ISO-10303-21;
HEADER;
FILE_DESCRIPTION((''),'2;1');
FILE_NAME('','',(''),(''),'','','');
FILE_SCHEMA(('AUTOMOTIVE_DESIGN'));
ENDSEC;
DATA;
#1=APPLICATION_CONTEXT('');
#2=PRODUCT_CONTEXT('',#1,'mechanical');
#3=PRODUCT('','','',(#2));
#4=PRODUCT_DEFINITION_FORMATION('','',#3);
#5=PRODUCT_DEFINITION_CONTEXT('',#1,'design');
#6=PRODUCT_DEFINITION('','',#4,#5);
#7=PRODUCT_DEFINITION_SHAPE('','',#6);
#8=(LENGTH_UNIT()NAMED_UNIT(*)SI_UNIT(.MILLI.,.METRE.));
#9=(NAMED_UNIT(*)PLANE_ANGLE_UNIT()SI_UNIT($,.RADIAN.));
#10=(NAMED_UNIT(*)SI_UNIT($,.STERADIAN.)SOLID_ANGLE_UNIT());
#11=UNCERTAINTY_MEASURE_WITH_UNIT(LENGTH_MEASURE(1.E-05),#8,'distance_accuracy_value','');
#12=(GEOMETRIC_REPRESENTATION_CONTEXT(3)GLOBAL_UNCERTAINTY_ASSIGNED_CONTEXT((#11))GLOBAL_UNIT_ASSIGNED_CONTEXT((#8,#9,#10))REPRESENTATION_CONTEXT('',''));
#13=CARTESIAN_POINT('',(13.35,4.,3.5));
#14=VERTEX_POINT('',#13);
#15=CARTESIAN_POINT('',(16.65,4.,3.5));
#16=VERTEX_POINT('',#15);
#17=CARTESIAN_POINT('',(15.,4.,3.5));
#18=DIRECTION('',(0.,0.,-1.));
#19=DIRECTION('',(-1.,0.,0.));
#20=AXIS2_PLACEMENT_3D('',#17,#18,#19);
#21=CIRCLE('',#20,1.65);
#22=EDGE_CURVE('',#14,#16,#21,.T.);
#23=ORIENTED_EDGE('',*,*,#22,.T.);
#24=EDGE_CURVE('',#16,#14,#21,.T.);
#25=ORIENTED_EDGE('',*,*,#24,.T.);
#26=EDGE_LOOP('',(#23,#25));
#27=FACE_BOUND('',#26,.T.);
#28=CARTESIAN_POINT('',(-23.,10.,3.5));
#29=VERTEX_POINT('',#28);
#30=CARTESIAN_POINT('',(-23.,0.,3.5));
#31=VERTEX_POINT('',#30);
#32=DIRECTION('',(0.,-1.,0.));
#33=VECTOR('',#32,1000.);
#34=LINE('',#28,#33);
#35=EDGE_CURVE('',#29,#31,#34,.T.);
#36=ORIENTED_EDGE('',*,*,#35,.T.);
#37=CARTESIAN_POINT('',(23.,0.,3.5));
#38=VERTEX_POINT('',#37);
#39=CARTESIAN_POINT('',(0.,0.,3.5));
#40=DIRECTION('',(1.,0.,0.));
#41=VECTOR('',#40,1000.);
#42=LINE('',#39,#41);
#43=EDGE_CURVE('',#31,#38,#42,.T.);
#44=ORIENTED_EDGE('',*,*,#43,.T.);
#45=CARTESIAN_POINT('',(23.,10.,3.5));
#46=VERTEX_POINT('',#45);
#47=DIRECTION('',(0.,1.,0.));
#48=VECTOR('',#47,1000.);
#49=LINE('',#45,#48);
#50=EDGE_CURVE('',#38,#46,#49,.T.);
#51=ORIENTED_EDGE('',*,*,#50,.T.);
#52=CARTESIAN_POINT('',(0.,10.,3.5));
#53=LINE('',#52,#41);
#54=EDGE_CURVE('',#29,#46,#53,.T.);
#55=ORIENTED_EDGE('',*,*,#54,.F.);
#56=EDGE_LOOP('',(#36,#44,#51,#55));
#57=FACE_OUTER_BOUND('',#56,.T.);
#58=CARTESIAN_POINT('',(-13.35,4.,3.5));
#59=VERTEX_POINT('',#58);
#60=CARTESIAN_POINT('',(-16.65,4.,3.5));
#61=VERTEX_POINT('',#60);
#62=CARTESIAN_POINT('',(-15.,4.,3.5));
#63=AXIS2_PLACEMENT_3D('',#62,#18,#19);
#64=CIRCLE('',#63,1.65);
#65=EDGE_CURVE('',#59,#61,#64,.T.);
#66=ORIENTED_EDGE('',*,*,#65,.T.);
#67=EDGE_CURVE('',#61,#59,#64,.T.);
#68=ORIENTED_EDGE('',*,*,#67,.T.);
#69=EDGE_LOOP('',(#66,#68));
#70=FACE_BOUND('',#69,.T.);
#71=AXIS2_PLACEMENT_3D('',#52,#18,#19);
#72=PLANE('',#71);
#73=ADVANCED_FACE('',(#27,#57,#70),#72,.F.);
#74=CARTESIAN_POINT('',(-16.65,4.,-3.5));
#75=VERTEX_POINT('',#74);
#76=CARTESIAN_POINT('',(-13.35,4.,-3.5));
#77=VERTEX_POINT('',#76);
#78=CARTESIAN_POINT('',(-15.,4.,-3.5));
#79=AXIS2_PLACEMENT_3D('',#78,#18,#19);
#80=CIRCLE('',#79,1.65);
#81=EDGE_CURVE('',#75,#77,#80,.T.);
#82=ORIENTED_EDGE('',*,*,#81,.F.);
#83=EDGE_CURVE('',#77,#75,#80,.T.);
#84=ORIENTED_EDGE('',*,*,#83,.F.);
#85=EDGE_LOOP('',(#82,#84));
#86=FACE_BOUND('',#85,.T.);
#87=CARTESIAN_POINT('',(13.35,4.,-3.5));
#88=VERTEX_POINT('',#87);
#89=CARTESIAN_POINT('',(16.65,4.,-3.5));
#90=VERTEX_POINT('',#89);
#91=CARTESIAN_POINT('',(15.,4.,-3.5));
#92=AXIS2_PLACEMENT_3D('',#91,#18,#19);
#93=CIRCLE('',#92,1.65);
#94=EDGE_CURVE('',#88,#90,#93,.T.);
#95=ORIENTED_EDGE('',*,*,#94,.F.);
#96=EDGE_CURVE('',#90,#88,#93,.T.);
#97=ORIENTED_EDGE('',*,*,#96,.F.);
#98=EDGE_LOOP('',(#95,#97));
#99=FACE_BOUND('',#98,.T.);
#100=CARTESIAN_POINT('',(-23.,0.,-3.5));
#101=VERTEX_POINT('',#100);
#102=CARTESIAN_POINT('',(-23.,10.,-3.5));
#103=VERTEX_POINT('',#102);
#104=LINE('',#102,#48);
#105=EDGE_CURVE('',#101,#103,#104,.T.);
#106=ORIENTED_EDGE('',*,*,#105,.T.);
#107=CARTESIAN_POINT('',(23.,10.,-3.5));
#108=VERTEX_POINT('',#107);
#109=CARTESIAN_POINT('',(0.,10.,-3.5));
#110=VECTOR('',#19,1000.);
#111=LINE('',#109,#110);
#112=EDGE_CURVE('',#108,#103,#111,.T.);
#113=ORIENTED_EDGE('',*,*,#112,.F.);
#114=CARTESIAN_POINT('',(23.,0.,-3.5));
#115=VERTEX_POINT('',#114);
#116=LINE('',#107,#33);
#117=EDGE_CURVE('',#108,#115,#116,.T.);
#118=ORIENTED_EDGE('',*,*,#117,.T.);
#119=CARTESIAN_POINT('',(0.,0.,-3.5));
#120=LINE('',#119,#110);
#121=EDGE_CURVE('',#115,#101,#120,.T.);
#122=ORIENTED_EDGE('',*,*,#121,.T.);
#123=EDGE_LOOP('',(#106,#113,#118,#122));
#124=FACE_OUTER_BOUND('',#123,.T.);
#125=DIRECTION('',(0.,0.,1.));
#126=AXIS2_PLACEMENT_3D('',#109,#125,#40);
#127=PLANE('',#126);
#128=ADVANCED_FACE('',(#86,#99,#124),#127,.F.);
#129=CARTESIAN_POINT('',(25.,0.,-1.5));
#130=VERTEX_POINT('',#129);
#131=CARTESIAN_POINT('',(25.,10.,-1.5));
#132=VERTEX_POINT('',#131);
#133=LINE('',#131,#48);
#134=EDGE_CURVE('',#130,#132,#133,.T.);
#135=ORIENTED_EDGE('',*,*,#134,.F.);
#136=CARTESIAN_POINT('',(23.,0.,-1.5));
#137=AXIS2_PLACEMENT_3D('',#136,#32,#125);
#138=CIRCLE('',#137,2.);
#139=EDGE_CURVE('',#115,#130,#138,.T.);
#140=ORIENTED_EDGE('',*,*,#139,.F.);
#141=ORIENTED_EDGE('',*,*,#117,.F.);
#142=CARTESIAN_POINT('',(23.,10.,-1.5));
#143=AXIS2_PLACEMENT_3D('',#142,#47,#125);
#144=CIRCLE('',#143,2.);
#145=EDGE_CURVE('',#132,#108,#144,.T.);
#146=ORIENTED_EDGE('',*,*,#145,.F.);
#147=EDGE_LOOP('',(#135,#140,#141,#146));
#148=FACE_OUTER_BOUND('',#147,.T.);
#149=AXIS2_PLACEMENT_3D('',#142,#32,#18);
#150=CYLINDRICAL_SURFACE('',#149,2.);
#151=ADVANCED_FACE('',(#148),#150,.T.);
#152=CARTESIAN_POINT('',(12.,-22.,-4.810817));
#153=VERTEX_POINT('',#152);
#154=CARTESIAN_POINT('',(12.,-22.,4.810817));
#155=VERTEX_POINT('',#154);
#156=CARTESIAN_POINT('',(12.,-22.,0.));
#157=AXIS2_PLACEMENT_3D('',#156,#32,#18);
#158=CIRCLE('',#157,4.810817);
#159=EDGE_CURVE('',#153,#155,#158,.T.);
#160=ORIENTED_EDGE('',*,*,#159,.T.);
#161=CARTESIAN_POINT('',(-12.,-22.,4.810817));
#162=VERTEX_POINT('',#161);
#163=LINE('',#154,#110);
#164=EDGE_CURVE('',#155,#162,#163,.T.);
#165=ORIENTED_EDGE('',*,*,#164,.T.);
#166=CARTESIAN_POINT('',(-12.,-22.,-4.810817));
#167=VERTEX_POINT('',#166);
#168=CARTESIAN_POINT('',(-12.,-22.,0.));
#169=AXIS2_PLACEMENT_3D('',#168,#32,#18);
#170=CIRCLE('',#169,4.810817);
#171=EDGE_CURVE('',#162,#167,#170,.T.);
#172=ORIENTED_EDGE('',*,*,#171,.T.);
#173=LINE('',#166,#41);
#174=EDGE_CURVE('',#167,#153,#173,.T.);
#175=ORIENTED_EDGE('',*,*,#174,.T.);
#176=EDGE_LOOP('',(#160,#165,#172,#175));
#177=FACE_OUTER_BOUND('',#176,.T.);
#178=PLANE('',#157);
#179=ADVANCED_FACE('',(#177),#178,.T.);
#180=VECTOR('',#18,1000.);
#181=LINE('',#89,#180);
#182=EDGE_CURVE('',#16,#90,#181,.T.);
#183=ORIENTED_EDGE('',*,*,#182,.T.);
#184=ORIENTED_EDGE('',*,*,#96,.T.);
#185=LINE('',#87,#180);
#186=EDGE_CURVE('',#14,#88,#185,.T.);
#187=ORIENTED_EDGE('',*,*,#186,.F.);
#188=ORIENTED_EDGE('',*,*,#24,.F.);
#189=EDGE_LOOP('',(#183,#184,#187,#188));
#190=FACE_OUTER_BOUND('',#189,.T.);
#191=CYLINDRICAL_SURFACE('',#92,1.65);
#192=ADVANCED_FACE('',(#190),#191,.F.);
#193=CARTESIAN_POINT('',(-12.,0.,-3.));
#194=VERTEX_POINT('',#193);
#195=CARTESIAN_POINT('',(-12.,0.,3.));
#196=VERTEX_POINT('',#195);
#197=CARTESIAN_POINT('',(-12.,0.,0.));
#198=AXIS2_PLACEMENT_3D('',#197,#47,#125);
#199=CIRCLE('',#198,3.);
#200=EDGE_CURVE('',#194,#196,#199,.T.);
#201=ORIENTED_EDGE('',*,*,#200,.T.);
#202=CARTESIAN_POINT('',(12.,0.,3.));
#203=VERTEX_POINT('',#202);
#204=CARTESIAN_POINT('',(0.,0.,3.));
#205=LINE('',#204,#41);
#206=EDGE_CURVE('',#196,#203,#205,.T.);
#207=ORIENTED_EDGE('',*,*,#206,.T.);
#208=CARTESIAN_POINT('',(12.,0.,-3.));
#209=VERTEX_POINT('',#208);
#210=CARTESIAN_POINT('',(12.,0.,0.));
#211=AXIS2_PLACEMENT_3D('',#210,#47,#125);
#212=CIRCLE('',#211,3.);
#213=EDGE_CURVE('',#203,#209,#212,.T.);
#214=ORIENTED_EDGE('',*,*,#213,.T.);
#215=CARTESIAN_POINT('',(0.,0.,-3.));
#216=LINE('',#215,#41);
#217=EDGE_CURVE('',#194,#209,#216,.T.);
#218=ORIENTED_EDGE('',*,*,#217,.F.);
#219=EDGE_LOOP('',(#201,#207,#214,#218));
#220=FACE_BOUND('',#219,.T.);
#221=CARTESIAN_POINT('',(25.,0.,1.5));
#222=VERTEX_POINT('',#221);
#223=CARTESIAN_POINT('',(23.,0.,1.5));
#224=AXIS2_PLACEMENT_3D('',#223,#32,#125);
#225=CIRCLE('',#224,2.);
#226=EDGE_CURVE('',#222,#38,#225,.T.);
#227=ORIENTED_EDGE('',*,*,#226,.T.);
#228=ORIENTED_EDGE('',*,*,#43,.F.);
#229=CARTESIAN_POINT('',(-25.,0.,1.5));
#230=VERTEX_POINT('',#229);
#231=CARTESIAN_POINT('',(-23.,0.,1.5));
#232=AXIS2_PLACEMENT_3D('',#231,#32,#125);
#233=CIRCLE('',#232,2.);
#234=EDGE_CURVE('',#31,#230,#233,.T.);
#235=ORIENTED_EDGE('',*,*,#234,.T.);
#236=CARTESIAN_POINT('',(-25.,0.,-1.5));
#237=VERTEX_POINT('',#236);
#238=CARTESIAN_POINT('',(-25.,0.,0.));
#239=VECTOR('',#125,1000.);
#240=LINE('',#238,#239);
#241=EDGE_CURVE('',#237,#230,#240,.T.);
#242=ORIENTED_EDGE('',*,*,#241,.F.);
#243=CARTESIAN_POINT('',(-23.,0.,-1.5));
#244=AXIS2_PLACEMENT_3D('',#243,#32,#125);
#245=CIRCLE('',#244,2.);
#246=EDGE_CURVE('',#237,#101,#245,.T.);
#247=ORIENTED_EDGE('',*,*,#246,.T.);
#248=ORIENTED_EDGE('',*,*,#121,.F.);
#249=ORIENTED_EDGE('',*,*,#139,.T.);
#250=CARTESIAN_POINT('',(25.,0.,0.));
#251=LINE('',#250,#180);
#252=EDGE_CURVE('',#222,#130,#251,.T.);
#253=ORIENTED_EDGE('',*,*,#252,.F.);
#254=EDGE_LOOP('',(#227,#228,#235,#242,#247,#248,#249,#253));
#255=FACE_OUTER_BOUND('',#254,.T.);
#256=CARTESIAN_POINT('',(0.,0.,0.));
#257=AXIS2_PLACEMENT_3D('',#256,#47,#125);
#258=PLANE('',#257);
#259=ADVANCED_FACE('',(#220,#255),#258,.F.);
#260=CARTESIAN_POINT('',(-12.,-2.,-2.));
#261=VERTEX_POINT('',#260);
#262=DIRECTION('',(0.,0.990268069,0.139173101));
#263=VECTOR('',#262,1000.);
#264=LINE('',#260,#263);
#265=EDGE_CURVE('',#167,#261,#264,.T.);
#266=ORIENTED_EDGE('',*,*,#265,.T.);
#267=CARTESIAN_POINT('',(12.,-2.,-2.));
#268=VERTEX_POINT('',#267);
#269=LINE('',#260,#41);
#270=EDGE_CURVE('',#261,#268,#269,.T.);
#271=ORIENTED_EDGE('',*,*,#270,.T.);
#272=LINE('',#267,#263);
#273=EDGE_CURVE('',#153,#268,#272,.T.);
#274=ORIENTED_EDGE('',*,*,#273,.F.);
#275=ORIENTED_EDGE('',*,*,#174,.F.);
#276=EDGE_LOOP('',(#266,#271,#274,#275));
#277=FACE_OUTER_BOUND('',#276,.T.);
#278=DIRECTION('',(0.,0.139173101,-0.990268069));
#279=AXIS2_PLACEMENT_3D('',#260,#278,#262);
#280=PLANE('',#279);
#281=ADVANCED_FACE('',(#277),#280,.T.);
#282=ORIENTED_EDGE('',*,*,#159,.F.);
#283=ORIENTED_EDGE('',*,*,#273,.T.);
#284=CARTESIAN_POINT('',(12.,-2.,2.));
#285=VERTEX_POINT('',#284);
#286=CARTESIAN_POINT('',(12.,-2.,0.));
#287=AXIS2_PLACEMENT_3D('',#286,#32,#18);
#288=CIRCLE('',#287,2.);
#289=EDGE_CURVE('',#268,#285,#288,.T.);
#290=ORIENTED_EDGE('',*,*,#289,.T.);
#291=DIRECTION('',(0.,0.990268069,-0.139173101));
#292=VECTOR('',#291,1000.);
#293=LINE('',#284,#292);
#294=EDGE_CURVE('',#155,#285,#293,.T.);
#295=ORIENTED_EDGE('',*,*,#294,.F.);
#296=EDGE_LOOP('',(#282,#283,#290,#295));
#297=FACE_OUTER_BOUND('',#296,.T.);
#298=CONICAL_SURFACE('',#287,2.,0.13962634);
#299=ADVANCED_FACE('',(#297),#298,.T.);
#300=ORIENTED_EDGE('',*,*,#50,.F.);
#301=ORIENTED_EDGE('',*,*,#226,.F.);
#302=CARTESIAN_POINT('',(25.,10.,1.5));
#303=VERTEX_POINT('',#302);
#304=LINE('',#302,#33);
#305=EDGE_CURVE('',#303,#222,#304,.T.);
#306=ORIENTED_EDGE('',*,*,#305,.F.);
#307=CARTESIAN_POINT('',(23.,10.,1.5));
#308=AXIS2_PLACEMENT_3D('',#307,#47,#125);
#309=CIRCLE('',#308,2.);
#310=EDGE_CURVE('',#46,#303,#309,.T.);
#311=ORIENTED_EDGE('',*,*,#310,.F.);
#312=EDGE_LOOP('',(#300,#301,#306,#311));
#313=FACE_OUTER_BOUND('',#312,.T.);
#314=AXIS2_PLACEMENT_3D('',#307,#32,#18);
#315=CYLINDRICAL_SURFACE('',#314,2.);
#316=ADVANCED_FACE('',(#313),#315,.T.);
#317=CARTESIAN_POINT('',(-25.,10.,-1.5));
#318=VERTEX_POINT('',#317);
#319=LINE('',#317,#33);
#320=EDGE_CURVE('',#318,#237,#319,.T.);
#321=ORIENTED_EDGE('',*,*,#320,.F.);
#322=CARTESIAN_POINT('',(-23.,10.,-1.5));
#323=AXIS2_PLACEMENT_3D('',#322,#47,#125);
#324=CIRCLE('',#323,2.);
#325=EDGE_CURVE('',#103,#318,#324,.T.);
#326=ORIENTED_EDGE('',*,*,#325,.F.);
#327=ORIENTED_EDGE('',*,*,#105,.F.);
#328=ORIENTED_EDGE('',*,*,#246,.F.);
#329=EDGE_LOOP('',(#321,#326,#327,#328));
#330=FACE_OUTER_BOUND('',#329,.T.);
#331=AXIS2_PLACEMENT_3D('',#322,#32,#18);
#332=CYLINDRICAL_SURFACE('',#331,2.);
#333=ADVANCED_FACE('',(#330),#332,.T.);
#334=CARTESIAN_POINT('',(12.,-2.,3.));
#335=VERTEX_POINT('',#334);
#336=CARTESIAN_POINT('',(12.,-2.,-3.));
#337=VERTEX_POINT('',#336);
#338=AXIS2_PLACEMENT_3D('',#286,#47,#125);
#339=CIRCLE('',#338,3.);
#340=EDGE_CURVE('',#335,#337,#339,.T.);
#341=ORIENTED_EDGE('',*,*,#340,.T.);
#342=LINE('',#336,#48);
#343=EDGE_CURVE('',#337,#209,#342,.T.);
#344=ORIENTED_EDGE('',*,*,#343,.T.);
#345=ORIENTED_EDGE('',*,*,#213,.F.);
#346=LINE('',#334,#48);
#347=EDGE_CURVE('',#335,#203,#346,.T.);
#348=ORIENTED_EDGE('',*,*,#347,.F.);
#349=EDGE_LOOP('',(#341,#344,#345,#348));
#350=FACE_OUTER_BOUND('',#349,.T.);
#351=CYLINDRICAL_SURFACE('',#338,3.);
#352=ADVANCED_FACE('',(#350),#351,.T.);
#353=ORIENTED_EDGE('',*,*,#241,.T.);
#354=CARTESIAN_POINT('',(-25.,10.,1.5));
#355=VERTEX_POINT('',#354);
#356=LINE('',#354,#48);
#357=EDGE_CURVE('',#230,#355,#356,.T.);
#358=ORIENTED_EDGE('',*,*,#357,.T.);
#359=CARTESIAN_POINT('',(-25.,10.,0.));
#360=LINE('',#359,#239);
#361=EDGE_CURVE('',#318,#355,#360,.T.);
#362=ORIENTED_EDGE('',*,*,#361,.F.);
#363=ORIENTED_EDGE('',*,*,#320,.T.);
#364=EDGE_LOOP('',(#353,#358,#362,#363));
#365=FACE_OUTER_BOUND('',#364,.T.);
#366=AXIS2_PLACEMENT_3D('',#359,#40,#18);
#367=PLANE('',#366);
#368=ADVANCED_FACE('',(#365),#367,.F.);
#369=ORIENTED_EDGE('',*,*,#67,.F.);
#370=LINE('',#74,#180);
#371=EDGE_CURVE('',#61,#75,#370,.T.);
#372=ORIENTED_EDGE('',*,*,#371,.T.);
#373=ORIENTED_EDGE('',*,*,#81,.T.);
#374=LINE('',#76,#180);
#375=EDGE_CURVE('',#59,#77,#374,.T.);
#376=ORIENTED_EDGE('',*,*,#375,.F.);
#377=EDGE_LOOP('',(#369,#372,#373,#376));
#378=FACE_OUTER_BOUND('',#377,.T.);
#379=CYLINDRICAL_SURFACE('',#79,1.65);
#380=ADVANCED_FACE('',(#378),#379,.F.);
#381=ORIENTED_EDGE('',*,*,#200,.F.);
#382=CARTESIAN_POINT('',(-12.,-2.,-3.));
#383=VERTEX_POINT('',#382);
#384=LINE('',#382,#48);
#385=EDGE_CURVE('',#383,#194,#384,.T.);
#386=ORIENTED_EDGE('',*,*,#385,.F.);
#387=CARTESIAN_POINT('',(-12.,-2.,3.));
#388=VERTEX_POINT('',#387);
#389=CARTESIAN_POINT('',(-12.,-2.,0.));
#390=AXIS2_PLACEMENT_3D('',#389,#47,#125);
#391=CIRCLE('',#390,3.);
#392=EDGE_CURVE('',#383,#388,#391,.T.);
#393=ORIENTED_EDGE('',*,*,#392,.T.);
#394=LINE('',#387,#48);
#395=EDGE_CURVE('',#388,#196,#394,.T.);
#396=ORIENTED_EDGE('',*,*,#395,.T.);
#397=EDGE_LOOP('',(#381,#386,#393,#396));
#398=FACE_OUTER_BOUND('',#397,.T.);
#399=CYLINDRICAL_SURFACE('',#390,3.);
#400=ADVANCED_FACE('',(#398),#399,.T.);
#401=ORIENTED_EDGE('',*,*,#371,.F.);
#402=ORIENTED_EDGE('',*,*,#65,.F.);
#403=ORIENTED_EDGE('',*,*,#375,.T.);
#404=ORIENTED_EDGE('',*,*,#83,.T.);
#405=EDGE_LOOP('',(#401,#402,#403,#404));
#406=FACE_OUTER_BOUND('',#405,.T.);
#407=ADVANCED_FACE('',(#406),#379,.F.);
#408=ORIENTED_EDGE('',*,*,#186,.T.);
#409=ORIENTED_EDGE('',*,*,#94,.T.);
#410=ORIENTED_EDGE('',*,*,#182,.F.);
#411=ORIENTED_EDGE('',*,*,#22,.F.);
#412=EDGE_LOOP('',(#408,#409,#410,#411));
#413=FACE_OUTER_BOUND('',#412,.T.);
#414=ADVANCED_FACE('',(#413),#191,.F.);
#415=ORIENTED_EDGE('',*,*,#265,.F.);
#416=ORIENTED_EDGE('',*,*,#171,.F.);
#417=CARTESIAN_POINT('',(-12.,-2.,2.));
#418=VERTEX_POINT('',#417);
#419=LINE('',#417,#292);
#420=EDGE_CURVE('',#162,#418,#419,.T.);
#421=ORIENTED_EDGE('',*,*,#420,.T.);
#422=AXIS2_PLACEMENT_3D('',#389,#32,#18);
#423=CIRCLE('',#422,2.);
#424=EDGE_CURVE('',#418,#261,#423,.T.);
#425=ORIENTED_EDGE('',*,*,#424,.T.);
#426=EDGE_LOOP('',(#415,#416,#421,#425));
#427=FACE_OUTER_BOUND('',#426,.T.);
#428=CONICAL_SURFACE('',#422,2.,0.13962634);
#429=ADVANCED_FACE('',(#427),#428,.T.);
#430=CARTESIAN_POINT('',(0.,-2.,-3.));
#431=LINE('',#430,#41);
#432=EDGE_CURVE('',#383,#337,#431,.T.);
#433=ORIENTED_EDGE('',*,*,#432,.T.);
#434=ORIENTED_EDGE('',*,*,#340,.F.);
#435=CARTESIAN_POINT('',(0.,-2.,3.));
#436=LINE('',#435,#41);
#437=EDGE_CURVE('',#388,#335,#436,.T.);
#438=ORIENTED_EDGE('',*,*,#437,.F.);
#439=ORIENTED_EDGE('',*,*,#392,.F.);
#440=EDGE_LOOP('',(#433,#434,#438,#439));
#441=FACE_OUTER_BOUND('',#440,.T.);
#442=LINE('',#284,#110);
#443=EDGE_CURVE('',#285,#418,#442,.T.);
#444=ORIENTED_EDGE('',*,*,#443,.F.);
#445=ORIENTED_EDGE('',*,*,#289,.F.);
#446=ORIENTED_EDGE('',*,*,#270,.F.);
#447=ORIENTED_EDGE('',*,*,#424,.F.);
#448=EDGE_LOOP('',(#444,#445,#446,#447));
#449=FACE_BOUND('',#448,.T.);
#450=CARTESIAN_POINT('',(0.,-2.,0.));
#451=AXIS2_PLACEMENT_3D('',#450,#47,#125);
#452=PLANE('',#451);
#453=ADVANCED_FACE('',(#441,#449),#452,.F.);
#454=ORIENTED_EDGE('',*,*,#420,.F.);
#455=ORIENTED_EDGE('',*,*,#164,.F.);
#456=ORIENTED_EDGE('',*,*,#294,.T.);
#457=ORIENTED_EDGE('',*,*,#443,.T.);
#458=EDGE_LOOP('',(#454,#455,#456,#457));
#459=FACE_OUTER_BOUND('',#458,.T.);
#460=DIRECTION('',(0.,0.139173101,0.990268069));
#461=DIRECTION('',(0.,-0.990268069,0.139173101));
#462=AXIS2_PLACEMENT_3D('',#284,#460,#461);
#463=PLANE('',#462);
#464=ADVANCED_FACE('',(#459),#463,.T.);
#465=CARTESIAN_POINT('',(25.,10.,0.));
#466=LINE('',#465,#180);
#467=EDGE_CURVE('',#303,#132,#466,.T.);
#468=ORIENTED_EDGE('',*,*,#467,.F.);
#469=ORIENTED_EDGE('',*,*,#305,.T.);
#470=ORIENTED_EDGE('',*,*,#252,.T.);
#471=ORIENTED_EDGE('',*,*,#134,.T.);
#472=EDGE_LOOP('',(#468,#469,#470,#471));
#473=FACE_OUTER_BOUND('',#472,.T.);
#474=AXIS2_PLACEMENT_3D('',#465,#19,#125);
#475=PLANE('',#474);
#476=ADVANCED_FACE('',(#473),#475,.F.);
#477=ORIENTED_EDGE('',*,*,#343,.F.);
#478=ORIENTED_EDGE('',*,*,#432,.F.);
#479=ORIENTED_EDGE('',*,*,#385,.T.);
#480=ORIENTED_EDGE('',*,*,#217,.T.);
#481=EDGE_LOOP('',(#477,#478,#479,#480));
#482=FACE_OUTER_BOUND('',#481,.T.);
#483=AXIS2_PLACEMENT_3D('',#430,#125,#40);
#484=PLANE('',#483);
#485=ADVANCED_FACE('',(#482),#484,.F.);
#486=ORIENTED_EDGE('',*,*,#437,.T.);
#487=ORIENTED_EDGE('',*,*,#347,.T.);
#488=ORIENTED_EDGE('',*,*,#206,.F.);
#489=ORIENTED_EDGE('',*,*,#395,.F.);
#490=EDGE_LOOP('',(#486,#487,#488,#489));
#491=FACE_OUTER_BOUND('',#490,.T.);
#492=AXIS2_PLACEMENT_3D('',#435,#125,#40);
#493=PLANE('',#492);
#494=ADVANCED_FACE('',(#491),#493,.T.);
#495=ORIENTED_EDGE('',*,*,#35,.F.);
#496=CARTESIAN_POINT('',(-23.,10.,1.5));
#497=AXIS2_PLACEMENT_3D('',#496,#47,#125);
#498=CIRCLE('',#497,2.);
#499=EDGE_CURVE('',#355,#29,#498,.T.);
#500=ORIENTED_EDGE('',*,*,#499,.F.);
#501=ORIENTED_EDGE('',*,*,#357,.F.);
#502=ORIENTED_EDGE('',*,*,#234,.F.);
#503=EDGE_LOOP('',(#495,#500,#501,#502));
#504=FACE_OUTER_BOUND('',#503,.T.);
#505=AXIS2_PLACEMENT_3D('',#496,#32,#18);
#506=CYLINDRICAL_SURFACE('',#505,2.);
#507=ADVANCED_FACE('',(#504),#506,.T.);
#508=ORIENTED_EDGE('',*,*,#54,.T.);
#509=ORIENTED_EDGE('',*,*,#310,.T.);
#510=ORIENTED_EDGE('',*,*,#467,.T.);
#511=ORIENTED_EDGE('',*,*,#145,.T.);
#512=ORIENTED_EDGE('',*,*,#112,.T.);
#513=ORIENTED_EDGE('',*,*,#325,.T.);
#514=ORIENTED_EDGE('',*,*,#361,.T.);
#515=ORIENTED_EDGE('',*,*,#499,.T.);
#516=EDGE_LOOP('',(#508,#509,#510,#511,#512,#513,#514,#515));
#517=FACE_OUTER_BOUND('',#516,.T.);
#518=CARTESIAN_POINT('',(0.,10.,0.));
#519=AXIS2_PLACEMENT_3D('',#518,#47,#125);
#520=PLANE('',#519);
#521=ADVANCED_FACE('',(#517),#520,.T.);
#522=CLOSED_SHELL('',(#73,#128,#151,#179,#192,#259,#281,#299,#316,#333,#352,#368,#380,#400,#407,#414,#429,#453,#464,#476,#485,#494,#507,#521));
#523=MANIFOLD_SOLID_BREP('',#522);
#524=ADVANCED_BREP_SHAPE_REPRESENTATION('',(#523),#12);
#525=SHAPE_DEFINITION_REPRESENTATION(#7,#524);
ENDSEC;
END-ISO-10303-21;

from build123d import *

# Parameters (mm, degrees)
SKETCH_1_3_W          = 50
SKETCH_1_3_H          = 7
BOSS_EXTRUDE1_DEPTH   = 10
BOSS_EXTRUDE2_DEPTH   = 2
BOSS_EXTRUDE3_DEPTH   = 20
BOSS_EXTRUDE3_DRAFT   = -8
FILLET1_R             = 2
M4_TAPPED_HOLE1_D     = 3.3
M4_TAPPED_HOLE1_DEPTH = 10.1
M4_TAPPED_HOLE1_TIP   = 0.991420021


with BuildPart() as part:
    # Sketch 1_3 → Boss-Extrude1 (new body)
    with BuildSketch(Plane(origin=(0, 0, 0), x_dir=(1, 0, 0), z_dir=(0, 1, 0))):
        Rectangle(SKETCH_1_3_W, SKETCH_1_3_H)
    extrude(amount=BOSS_EXTRUDE1_DEPTH)

    # Sketch 1_3 2 → Boss-Extrude2 (add)
    with BuildSketch(Plane(origin=(0, 0, 0), x_dir=(1, 0, 0), z_dir=(0, 1, 0))):
        with BuildLine():
            Line((-12, 3), (12, 3))
            ThreePointArc((12, 3), (15, 0), (12, -3))
            Line((12, -3), (-12, -3))
            ThreePointArc((-12, -3), (-15, 0), (-12, 3))
        make_face()
    extrude(amount=-BOSS_EXTRUDE2_DEPTH)


with BuildPart() as boss_extrude3_tool:
    # Sketch2 → Boss-Extrude3 (with draft: the straight prism first)
    with BuildSketch(Plane.XZ.offset(2)):
        with BuildLine():
            Line((12, 2), (-12, 2))
            ThreePointArc((-12, 2), (-14, 0), (-12, -2))
            Line((-12, -2), (12, -2))
            ThreePointArc((12, -2), (14, 0), (12, 2))
        make_face()
    extrude(amount=BOSS_EXTRUDE3_DEPTH)
    # Boss-Extrude3: the draft: its side faces are tilted about the plane it starts from
    boss_extrude3_sides = [boss_extrude3_tool.faces().sort_by_distance(p)[0] for p in [
        (0, -12, 2),
        (-14, -12, 0),
        (0, -12, -2),
        (14, -12, 0),
    ]]
    draft(boss_extrude3_sides, Plane.XZ.offset(2), BOSS_EXTRUDE3_DRAFT)


with BuildPart() as part_1:
    add(part.part)

    # Boss-Extrude3: add boss_extrude3_tool
    add(boss_extrude3_tool.part)

    # Fillet1
    fillet1_edges = [part_1.edges().sort_by_distance(p)[0] for p in [
        (-25, 5, 3.5),
        (-25, 5, -3.5),
        (25, 5, -3.5),
        (25, 5, 3.5),
    ]]
    fillet(fillet1_edges, radius=FILLET1_R)

    # M4 Tapped Hole1
    with Locations(Plane(origin=(15, 4, -3.5), x_dir=(-1, 0, 0), z_dir=(0, 0, -1))):
        with Locations((0, 0), (30, 0)):
            Hole(M4_TAPPED_HOLE1_D / 2, depth=M4_TAPPED_HOLE1_DEPTH)
            with Locations((0, 0, -(M4_TAPPED_HOLE1_DEPTH + M4_TAPPED_HOLE1_TIP / 2))):  # 118° drill point
                Cone(0, M4_TAPPED_HOLE1_D / 2, M4_TAPPED_HOLE1_TIP, mode=Mode.SUBTRACT)


solid = part_1.part
